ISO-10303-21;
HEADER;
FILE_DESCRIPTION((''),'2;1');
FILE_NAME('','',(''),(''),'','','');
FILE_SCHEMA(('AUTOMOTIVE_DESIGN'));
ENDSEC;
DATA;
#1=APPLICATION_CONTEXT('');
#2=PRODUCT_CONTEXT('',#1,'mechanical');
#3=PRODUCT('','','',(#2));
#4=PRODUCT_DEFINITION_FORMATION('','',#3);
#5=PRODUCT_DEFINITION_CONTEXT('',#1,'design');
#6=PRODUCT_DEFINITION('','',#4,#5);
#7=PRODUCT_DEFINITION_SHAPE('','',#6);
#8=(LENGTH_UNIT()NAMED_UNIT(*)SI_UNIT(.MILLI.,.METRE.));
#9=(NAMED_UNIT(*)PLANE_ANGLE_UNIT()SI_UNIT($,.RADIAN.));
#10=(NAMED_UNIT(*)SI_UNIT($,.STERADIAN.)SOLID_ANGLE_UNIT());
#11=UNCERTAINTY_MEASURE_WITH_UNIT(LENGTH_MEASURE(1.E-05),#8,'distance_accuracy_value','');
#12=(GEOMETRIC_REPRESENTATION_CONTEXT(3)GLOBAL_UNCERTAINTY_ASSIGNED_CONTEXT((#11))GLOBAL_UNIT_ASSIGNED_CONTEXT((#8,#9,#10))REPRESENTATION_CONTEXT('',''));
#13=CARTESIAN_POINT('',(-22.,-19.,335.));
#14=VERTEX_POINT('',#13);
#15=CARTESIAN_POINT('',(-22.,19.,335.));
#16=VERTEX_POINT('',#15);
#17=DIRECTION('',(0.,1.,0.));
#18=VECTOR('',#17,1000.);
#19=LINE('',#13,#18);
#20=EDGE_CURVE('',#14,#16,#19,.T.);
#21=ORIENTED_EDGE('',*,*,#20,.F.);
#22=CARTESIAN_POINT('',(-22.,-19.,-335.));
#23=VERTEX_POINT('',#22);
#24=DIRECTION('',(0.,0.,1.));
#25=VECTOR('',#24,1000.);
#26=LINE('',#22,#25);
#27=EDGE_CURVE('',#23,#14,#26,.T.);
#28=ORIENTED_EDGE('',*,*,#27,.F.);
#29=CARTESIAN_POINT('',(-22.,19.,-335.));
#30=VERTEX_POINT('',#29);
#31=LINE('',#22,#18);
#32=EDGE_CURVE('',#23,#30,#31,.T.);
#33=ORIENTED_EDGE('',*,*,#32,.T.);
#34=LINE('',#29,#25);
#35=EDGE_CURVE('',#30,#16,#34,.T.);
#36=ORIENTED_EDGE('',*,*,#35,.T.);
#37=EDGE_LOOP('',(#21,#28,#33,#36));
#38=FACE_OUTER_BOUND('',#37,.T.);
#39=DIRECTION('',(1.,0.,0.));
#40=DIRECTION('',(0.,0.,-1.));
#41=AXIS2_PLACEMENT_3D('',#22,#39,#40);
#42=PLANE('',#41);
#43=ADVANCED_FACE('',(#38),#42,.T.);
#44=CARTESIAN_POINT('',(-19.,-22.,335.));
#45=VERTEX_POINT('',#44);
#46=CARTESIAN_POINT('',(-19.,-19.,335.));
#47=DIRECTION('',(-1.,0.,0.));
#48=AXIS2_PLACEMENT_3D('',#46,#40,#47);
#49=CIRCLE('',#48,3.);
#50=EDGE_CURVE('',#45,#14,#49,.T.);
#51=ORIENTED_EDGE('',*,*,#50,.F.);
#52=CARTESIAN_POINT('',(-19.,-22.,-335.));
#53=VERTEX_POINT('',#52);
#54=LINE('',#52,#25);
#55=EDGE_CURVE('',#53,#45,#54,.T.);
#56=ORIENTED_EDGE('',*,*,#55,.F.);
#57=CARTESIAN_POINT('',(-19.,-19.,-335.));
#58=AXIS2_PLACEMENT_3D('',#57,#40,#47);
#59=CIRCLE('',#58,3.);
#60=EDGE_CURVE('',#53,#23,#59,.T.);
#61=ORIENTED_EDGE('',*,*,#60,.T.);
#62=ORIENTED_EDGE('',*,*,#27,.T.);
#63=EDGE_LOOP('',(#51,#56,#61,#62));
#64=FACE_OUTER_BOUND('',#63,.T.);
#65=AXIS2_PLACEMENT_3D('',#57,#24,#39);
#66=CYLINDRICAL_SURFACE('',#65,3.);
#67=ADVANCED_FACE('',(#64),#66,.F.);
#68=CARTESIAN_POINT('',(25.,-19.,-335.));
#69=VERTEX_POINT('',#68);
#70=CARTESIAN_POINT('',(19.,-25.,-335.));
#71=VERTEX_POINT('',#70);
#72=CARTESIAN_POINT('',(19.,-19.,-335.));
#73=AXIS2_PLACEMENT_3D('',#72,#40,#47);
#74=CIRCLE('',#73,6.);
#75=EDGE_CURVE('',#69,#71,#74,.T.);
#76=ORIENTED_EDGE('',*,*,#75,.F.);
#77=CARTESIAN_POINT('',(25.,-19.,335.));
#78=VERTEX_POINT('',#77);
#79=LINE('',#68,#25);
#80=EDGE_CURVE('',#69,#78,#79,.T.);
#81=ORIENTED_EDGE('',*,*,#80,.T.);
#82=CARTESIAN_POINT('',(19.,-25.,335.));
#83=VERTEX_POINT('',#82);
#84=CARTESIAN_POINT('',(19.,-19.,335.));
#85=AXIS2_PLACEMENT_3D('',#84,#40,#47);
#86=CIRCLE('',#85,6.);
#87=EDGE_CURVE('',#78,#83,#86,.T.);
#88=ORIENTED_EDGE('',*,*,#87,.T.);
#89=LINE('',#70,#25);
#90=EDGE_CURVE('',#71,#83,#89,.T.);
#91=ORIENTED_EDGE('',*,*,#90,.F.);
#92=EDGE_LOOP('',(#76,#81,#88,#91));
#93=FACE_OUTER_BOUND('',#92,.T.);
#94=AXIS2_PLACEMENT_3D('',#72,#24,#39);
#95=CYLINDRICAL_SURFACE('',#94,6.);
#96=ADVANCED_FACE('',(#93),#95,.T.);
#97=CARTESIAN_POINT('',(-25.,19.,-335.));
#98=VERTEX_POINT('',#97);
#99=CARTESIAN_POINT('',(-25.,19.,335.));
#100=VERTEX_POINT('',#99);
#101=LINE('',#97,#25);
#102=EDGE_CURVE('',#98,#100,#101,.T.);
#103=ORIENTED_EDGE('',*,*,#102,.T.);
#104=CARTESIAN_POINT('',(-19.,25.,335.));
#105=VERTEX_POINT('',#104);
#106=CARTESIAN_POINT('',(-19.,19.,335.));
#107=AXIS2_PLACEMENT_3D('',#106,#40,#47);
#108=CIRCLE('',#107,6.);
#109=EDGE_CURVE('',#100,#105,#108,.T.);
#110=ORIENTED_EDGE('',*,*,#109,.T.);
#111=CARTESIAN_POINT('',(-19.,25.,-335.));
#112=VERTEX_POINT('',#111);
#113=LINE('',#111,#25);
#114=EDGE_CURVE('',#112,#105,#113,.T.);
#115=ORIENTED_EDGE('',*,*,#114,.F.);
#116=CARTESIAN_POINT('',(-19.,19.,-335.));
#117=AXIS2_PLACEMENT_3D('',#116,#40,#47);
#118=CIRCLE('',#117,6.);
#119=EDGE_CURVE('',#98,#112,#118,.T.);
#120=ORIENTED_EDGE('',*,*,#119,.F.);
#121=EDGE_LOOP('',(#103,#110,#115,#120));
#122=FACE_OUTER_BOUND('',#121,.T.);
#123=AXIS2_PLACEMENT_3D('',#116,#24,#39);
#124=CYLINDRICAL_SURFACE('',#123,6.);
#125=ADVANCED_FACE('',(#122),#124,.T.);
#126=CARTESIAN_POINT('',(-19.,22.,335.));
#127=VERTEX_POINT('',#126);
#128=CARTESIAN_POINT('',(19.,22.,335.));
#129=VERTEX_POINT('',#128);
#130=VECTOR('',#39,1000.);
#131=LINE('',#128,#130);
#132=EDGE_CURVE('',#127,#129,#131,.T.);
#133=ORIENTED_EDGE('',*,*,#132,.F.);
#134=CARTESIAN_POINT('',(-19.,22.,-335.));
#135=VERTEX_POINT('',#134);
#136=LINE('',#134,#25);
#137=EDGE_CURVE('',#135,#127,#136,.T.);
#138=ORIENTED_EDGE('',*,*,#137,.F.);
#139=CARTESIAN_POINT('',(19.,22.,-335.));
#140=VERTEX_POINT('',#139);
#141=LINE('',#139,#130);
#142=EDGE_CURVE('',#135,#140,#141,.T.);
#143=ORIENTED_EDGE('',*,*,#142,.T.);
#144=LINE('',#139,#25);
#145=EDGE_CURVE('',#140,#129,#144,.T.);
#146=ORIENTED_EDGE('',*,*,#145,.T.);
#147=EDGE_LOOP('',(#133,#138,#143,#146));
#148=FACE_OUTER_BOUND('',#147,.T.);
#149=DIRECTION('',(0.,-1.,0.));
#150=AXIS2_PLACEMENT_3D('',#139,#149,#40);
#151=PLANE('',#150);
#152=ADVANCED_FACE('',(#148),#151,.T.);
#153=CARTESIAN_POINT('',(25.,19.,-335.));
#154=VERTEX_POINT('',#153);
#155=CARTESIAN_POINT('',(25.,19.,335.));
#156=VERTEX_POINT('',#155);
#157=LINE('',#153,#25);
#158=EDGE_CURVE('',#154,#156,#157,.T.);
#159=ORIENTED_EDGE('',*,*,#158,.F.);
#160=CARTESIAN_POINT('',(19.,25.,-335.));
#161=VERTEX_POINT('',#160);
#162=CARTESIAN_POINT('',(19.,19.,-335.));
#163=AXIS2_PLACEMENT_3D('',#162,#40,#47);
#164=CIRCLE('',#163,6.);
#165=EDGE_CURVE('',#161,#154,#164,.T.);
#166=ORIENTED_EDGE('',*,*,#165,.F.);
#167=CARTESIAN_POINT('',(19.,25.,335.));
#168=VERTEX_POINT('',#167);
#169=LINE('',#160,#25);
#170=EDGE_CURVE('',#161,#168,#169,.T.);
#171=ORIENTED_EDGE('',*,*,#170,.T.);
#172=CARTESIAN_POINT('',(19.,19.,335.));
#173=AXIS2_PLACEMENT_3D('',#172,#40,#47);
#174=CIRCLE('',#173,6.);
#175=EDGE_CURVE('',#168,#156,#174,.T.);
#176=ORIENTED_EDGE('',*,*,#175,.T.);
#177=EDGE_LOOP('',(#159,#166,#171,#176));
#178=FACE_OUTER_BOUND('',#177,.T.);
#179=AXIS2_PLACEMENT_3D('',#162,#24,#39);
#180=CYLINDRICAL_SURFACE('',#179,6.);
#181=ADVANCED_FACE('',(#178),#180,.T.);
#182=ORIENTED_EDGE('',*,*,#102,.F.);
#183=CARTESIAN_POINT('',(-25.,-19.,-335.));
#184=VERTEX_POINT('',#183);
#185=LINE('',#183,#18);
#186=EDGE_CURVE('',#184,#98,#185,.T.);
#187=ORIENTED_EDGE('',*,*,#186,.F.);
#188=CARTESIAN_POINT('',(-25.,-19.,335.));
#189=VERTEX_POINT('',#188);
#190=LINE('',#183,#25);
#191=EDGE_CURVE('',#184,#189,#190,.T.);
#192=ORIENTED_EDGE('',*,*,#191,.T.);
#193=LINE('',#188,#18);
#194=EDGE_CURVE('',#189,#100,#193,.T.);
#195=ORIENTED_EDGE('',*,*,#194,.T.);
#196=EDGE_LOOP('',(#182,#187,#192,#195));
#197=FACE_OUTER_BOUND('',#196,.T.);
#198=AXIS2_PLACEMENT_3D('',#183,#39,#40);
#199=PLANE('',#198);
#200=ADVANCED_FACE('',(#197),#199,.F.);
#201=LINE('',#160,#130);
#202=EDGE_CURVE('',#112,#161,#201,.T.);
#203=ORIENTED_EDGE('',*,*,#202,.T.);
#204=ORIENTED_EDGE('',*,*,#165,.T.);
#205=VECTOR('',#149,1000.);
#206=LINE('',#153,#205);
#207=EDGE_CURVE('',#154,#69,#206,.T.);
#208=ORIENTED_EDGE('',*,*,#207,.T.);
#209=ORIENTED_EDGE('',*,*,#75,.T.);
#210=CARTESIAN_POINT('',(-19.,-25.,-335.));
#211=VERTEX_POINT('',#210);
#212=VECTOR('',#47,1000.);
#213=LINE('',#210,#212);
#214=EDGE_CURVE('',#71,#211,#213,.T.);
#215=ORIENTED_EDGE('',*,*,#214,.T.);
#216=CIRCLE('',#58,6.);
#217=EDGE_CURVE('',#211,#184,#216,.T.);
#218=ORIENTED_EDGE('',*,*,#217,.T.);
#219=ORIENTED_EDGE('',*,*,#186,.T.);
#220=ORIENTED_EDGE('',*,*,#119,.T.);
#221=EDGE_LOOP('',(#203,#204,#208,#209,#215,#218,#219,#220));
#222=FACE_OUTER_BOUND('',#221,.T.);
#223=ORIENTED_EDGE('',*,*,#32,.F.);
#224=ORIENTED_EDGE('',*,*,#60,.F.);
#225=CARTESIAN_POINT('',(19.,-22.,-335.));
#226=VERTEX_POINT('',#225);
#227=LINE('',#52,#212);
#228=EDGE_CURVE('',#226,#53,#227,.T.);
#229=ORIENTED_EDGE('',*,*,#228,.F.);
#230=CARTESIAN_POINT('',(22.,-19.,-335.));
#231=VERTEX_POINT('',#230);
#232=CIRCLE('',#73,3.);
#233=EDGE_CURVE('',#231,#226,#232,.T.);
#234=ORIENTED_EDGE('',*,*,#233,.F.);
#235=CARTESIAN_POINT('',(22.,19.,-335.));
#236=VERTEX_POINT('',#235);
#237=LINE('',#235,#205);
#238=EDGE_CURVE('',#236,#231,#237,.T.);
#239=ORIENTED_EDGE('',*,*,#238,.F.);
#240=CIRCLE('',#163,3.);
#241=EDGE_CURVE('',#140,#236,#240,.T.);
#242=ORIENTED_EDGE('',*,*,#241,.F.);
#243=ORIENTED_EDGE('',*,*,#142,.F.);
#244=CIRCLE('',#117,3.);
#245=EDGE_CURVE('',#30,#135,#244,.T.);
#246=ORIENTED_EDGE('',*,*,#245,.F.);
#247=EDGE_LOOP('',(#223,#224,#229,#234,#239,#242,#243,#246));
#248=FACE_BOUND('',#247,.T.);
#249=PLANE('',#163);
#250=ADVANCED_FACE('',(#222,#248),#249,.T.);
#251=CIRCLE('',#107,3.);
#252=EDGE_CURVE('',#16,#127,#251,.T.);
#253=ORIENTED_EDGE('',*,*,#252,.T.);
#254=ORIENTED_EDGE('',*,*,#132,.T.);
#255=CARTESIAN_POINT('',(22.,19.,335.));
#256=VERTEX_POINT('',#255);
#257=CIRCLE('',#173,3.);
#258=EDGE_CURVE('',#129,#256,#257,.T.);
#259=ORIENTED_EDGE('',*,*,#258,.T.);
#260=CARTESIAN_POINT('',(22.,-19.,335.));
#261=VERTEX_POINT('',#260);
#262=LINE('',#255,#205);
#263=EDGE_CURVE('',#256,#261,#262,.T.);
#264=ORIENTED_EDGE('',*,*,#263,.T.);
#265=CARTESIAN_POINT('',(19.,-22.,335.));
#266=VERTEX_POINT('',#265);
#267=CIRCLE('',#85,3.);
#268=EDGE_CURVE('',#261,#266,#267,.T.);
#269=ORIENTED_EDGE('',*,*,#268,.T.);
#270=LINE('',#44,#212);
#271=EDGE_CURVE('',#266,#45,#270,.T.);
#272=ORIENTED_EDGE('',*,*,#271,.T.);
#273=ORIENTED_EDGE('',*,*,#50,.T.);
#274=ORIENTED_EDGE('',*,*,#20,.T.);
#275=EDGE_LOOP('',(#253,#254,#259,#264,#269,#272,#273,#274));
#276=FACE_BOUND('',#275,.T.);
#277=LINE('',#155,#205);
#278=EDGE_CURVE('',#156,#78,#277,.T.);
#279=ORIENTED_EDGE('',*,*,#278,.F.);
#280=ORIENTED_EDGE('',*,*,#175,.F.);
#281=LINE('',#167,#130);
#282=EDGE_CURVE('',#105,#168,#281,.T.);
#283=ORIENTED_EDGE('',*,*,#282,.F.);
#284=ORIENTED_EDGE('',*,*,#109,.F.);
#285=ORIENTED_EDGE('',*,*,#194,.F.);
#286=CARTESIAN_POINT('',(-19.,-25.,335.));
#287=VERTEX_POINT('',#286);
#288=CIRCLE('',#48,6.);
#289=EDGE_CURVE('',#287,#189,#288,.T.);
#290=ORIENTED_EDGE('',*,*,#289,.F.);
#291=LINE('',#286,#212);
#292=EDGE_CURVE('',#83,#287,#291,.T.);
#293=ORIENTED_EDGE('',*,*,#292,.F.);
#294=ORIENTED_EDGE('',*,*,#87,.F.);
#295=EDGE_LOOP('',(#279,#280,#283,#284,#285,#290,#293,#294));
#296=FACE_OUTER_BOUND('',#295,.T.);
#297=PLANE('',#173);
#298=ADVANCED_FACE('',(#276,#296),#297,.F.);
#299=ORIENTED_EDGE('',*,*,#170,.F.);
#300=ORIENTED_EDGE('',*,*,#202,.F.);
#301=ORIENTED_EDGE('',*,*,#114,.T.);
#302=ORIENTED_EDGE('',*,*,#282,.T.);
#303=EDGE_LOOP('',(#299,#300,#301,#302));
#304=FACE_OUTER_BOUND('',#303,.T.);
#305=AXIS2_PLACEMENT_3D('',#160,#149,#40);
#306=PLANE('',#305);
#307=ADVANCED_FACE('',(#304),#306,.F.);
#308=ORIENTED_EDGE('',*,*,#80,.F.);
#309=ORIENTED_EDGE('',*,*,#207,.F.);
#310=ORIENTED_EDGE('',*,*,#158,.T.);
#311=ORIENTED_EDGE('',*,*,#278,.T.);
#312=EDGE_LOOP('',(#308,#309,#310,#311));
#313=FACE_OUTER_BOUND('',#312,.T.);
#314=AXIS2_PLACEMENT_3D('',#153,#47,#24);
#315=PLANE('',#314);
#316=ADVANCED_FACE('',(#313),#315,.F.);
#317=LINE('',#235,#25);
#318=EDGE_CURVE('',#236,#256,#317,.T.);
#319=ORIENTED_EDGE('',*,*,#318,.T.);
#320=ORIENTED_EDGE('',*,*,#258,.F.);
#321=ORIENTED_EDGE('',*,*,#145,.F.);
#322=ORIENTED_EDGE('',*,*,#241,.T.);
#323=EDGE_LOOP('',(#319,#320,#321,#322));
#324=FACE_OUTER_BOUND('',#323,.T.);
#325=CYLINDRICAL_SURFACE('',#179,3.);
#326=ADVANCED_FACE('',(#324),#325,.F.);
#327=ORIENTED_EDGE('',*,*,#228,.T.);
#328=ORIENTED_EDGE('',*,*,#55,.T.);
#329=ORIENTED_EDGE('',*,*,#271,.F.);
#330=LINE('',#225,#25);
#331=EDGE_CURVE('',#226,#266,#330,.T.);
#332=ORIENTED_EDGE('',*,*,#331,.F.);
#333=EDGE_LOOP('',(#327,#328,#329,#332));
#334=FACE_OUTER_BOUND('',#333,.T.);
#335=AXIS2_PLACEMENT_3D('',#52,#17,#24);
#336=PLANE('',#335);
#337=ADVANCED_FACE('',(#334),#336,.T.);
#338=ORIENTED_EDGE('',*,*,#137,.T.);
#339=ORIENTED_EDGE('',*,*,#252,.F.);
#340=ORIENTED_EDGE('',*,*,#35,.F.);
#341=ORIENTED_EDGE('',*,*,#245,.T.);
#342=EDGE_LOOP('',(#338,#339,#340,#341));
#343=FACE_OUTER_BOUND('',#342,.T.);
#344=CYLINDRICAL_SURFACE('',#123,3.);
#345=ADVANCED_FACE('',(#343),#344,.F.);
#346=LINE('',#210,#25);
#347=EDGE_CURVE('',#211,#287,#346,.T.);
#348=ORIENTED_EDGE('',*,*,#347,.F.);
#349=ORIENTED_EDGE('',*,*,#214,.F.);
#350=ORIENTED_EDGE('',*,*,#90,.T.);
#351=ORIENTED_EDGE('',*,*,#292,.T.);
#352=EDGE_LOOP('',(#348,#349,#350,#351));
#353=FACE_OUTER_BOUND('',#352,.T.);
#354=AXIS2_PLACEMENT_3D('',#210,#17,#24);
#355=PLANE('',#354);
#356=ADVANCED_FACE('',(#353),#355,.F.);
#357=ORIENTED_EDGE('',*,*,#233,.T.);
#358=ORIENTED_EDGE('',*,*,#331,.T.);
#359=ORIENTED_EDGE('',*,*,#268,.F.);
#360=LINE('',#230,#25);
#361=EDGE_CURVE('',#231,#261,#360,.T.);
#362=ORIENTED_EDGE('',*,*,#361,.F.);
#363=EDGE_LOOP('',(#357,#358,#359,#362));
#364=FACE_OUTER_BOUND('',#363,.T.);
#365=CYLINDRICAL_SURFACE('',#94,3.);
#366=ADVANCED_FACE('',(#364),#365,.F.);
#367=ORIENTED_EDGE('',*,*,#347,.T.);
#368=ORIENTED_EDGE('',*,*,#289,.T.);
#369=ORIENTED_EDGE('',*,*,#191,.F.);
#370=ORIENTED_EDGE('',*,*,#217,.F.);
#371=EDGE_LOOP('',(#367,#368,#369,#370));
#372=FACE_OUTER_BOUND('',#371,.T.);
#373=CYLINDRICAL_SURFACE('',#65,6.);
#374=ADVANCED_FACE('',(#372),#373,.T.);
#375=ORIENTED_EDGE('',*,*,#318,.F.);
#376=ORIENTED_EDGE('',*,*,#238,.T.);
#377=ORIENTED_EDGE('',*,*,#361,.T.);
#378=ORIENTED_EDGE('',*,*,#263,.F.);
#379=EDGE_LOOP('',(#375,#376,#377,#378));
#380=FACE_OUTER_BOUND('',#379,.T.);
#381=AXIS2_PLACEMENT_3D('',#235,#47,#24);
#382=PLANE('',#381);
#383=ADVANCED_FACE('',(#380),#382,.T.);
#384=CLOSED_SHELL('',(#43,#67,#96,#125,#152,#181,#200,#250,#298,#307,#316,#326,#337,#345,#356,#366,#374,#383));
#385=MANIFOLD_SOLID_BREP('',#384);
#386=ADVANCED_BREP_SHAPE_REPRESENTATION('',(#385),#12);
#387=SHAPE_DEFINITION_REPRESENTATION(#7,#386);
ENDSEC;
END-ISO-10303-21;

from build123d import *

# Parameters (mm, degrees)
GB_6728_1986_050_X_50_X_3_1_DEPTH = 670


with BuildPart() as part:
    # Sketch1 → Gb／6728-1986方形空心型钢 050 X 50 X 3(1) (new body)
    with BuildSketch(Plane.YX.offset(-335)):
        with BuildLine():
            Line((-19, -25), (19, -25))
            ThreePointArc((19, -25), (23.242640687, -23.242640687), (25, -19))
            Line((25, -19), (25, 19))
            ThreePointArc((25, 19), (23.242640687, 23.242640687), (19, 25))
            Line((19, 25), (-19, 25))
            ThreePointArc((-19, 25), (-23.242640687, 23.242640687), (-25, 19))
            Line((-25, 19), (-25, -19))
            ThreePointArc((-25, -19), (-23.242640687, -23.242640687), (-19, -25))
        make_face()
        with BuildLine():
            Line((-19, -22), (19, -22))
            ThreePointArc((19, -22), (21.121320344, -21.121320344), (22, -19))
            Line((22, -19), (22, 19))
            ThreePointArc((22, 19), (21.121320344, 21.121320344), (19, 22))
            Line((19, 22), (-19, 22))
            ThreePointArc((-19, 22), (-21.121320344, 21.121320344), (-22, 19))
            Line((-22, 19), (-22, -19))
            ThreePointArc((-22, -19), (-21.121320344, -21.121320344), (-19, -22))
        make_face(mode=Mode.SUBTRACT)
    extrude(amount=GB_6728_1986_050_X_50_X_3_1_DEPTH)


solid = part.part
